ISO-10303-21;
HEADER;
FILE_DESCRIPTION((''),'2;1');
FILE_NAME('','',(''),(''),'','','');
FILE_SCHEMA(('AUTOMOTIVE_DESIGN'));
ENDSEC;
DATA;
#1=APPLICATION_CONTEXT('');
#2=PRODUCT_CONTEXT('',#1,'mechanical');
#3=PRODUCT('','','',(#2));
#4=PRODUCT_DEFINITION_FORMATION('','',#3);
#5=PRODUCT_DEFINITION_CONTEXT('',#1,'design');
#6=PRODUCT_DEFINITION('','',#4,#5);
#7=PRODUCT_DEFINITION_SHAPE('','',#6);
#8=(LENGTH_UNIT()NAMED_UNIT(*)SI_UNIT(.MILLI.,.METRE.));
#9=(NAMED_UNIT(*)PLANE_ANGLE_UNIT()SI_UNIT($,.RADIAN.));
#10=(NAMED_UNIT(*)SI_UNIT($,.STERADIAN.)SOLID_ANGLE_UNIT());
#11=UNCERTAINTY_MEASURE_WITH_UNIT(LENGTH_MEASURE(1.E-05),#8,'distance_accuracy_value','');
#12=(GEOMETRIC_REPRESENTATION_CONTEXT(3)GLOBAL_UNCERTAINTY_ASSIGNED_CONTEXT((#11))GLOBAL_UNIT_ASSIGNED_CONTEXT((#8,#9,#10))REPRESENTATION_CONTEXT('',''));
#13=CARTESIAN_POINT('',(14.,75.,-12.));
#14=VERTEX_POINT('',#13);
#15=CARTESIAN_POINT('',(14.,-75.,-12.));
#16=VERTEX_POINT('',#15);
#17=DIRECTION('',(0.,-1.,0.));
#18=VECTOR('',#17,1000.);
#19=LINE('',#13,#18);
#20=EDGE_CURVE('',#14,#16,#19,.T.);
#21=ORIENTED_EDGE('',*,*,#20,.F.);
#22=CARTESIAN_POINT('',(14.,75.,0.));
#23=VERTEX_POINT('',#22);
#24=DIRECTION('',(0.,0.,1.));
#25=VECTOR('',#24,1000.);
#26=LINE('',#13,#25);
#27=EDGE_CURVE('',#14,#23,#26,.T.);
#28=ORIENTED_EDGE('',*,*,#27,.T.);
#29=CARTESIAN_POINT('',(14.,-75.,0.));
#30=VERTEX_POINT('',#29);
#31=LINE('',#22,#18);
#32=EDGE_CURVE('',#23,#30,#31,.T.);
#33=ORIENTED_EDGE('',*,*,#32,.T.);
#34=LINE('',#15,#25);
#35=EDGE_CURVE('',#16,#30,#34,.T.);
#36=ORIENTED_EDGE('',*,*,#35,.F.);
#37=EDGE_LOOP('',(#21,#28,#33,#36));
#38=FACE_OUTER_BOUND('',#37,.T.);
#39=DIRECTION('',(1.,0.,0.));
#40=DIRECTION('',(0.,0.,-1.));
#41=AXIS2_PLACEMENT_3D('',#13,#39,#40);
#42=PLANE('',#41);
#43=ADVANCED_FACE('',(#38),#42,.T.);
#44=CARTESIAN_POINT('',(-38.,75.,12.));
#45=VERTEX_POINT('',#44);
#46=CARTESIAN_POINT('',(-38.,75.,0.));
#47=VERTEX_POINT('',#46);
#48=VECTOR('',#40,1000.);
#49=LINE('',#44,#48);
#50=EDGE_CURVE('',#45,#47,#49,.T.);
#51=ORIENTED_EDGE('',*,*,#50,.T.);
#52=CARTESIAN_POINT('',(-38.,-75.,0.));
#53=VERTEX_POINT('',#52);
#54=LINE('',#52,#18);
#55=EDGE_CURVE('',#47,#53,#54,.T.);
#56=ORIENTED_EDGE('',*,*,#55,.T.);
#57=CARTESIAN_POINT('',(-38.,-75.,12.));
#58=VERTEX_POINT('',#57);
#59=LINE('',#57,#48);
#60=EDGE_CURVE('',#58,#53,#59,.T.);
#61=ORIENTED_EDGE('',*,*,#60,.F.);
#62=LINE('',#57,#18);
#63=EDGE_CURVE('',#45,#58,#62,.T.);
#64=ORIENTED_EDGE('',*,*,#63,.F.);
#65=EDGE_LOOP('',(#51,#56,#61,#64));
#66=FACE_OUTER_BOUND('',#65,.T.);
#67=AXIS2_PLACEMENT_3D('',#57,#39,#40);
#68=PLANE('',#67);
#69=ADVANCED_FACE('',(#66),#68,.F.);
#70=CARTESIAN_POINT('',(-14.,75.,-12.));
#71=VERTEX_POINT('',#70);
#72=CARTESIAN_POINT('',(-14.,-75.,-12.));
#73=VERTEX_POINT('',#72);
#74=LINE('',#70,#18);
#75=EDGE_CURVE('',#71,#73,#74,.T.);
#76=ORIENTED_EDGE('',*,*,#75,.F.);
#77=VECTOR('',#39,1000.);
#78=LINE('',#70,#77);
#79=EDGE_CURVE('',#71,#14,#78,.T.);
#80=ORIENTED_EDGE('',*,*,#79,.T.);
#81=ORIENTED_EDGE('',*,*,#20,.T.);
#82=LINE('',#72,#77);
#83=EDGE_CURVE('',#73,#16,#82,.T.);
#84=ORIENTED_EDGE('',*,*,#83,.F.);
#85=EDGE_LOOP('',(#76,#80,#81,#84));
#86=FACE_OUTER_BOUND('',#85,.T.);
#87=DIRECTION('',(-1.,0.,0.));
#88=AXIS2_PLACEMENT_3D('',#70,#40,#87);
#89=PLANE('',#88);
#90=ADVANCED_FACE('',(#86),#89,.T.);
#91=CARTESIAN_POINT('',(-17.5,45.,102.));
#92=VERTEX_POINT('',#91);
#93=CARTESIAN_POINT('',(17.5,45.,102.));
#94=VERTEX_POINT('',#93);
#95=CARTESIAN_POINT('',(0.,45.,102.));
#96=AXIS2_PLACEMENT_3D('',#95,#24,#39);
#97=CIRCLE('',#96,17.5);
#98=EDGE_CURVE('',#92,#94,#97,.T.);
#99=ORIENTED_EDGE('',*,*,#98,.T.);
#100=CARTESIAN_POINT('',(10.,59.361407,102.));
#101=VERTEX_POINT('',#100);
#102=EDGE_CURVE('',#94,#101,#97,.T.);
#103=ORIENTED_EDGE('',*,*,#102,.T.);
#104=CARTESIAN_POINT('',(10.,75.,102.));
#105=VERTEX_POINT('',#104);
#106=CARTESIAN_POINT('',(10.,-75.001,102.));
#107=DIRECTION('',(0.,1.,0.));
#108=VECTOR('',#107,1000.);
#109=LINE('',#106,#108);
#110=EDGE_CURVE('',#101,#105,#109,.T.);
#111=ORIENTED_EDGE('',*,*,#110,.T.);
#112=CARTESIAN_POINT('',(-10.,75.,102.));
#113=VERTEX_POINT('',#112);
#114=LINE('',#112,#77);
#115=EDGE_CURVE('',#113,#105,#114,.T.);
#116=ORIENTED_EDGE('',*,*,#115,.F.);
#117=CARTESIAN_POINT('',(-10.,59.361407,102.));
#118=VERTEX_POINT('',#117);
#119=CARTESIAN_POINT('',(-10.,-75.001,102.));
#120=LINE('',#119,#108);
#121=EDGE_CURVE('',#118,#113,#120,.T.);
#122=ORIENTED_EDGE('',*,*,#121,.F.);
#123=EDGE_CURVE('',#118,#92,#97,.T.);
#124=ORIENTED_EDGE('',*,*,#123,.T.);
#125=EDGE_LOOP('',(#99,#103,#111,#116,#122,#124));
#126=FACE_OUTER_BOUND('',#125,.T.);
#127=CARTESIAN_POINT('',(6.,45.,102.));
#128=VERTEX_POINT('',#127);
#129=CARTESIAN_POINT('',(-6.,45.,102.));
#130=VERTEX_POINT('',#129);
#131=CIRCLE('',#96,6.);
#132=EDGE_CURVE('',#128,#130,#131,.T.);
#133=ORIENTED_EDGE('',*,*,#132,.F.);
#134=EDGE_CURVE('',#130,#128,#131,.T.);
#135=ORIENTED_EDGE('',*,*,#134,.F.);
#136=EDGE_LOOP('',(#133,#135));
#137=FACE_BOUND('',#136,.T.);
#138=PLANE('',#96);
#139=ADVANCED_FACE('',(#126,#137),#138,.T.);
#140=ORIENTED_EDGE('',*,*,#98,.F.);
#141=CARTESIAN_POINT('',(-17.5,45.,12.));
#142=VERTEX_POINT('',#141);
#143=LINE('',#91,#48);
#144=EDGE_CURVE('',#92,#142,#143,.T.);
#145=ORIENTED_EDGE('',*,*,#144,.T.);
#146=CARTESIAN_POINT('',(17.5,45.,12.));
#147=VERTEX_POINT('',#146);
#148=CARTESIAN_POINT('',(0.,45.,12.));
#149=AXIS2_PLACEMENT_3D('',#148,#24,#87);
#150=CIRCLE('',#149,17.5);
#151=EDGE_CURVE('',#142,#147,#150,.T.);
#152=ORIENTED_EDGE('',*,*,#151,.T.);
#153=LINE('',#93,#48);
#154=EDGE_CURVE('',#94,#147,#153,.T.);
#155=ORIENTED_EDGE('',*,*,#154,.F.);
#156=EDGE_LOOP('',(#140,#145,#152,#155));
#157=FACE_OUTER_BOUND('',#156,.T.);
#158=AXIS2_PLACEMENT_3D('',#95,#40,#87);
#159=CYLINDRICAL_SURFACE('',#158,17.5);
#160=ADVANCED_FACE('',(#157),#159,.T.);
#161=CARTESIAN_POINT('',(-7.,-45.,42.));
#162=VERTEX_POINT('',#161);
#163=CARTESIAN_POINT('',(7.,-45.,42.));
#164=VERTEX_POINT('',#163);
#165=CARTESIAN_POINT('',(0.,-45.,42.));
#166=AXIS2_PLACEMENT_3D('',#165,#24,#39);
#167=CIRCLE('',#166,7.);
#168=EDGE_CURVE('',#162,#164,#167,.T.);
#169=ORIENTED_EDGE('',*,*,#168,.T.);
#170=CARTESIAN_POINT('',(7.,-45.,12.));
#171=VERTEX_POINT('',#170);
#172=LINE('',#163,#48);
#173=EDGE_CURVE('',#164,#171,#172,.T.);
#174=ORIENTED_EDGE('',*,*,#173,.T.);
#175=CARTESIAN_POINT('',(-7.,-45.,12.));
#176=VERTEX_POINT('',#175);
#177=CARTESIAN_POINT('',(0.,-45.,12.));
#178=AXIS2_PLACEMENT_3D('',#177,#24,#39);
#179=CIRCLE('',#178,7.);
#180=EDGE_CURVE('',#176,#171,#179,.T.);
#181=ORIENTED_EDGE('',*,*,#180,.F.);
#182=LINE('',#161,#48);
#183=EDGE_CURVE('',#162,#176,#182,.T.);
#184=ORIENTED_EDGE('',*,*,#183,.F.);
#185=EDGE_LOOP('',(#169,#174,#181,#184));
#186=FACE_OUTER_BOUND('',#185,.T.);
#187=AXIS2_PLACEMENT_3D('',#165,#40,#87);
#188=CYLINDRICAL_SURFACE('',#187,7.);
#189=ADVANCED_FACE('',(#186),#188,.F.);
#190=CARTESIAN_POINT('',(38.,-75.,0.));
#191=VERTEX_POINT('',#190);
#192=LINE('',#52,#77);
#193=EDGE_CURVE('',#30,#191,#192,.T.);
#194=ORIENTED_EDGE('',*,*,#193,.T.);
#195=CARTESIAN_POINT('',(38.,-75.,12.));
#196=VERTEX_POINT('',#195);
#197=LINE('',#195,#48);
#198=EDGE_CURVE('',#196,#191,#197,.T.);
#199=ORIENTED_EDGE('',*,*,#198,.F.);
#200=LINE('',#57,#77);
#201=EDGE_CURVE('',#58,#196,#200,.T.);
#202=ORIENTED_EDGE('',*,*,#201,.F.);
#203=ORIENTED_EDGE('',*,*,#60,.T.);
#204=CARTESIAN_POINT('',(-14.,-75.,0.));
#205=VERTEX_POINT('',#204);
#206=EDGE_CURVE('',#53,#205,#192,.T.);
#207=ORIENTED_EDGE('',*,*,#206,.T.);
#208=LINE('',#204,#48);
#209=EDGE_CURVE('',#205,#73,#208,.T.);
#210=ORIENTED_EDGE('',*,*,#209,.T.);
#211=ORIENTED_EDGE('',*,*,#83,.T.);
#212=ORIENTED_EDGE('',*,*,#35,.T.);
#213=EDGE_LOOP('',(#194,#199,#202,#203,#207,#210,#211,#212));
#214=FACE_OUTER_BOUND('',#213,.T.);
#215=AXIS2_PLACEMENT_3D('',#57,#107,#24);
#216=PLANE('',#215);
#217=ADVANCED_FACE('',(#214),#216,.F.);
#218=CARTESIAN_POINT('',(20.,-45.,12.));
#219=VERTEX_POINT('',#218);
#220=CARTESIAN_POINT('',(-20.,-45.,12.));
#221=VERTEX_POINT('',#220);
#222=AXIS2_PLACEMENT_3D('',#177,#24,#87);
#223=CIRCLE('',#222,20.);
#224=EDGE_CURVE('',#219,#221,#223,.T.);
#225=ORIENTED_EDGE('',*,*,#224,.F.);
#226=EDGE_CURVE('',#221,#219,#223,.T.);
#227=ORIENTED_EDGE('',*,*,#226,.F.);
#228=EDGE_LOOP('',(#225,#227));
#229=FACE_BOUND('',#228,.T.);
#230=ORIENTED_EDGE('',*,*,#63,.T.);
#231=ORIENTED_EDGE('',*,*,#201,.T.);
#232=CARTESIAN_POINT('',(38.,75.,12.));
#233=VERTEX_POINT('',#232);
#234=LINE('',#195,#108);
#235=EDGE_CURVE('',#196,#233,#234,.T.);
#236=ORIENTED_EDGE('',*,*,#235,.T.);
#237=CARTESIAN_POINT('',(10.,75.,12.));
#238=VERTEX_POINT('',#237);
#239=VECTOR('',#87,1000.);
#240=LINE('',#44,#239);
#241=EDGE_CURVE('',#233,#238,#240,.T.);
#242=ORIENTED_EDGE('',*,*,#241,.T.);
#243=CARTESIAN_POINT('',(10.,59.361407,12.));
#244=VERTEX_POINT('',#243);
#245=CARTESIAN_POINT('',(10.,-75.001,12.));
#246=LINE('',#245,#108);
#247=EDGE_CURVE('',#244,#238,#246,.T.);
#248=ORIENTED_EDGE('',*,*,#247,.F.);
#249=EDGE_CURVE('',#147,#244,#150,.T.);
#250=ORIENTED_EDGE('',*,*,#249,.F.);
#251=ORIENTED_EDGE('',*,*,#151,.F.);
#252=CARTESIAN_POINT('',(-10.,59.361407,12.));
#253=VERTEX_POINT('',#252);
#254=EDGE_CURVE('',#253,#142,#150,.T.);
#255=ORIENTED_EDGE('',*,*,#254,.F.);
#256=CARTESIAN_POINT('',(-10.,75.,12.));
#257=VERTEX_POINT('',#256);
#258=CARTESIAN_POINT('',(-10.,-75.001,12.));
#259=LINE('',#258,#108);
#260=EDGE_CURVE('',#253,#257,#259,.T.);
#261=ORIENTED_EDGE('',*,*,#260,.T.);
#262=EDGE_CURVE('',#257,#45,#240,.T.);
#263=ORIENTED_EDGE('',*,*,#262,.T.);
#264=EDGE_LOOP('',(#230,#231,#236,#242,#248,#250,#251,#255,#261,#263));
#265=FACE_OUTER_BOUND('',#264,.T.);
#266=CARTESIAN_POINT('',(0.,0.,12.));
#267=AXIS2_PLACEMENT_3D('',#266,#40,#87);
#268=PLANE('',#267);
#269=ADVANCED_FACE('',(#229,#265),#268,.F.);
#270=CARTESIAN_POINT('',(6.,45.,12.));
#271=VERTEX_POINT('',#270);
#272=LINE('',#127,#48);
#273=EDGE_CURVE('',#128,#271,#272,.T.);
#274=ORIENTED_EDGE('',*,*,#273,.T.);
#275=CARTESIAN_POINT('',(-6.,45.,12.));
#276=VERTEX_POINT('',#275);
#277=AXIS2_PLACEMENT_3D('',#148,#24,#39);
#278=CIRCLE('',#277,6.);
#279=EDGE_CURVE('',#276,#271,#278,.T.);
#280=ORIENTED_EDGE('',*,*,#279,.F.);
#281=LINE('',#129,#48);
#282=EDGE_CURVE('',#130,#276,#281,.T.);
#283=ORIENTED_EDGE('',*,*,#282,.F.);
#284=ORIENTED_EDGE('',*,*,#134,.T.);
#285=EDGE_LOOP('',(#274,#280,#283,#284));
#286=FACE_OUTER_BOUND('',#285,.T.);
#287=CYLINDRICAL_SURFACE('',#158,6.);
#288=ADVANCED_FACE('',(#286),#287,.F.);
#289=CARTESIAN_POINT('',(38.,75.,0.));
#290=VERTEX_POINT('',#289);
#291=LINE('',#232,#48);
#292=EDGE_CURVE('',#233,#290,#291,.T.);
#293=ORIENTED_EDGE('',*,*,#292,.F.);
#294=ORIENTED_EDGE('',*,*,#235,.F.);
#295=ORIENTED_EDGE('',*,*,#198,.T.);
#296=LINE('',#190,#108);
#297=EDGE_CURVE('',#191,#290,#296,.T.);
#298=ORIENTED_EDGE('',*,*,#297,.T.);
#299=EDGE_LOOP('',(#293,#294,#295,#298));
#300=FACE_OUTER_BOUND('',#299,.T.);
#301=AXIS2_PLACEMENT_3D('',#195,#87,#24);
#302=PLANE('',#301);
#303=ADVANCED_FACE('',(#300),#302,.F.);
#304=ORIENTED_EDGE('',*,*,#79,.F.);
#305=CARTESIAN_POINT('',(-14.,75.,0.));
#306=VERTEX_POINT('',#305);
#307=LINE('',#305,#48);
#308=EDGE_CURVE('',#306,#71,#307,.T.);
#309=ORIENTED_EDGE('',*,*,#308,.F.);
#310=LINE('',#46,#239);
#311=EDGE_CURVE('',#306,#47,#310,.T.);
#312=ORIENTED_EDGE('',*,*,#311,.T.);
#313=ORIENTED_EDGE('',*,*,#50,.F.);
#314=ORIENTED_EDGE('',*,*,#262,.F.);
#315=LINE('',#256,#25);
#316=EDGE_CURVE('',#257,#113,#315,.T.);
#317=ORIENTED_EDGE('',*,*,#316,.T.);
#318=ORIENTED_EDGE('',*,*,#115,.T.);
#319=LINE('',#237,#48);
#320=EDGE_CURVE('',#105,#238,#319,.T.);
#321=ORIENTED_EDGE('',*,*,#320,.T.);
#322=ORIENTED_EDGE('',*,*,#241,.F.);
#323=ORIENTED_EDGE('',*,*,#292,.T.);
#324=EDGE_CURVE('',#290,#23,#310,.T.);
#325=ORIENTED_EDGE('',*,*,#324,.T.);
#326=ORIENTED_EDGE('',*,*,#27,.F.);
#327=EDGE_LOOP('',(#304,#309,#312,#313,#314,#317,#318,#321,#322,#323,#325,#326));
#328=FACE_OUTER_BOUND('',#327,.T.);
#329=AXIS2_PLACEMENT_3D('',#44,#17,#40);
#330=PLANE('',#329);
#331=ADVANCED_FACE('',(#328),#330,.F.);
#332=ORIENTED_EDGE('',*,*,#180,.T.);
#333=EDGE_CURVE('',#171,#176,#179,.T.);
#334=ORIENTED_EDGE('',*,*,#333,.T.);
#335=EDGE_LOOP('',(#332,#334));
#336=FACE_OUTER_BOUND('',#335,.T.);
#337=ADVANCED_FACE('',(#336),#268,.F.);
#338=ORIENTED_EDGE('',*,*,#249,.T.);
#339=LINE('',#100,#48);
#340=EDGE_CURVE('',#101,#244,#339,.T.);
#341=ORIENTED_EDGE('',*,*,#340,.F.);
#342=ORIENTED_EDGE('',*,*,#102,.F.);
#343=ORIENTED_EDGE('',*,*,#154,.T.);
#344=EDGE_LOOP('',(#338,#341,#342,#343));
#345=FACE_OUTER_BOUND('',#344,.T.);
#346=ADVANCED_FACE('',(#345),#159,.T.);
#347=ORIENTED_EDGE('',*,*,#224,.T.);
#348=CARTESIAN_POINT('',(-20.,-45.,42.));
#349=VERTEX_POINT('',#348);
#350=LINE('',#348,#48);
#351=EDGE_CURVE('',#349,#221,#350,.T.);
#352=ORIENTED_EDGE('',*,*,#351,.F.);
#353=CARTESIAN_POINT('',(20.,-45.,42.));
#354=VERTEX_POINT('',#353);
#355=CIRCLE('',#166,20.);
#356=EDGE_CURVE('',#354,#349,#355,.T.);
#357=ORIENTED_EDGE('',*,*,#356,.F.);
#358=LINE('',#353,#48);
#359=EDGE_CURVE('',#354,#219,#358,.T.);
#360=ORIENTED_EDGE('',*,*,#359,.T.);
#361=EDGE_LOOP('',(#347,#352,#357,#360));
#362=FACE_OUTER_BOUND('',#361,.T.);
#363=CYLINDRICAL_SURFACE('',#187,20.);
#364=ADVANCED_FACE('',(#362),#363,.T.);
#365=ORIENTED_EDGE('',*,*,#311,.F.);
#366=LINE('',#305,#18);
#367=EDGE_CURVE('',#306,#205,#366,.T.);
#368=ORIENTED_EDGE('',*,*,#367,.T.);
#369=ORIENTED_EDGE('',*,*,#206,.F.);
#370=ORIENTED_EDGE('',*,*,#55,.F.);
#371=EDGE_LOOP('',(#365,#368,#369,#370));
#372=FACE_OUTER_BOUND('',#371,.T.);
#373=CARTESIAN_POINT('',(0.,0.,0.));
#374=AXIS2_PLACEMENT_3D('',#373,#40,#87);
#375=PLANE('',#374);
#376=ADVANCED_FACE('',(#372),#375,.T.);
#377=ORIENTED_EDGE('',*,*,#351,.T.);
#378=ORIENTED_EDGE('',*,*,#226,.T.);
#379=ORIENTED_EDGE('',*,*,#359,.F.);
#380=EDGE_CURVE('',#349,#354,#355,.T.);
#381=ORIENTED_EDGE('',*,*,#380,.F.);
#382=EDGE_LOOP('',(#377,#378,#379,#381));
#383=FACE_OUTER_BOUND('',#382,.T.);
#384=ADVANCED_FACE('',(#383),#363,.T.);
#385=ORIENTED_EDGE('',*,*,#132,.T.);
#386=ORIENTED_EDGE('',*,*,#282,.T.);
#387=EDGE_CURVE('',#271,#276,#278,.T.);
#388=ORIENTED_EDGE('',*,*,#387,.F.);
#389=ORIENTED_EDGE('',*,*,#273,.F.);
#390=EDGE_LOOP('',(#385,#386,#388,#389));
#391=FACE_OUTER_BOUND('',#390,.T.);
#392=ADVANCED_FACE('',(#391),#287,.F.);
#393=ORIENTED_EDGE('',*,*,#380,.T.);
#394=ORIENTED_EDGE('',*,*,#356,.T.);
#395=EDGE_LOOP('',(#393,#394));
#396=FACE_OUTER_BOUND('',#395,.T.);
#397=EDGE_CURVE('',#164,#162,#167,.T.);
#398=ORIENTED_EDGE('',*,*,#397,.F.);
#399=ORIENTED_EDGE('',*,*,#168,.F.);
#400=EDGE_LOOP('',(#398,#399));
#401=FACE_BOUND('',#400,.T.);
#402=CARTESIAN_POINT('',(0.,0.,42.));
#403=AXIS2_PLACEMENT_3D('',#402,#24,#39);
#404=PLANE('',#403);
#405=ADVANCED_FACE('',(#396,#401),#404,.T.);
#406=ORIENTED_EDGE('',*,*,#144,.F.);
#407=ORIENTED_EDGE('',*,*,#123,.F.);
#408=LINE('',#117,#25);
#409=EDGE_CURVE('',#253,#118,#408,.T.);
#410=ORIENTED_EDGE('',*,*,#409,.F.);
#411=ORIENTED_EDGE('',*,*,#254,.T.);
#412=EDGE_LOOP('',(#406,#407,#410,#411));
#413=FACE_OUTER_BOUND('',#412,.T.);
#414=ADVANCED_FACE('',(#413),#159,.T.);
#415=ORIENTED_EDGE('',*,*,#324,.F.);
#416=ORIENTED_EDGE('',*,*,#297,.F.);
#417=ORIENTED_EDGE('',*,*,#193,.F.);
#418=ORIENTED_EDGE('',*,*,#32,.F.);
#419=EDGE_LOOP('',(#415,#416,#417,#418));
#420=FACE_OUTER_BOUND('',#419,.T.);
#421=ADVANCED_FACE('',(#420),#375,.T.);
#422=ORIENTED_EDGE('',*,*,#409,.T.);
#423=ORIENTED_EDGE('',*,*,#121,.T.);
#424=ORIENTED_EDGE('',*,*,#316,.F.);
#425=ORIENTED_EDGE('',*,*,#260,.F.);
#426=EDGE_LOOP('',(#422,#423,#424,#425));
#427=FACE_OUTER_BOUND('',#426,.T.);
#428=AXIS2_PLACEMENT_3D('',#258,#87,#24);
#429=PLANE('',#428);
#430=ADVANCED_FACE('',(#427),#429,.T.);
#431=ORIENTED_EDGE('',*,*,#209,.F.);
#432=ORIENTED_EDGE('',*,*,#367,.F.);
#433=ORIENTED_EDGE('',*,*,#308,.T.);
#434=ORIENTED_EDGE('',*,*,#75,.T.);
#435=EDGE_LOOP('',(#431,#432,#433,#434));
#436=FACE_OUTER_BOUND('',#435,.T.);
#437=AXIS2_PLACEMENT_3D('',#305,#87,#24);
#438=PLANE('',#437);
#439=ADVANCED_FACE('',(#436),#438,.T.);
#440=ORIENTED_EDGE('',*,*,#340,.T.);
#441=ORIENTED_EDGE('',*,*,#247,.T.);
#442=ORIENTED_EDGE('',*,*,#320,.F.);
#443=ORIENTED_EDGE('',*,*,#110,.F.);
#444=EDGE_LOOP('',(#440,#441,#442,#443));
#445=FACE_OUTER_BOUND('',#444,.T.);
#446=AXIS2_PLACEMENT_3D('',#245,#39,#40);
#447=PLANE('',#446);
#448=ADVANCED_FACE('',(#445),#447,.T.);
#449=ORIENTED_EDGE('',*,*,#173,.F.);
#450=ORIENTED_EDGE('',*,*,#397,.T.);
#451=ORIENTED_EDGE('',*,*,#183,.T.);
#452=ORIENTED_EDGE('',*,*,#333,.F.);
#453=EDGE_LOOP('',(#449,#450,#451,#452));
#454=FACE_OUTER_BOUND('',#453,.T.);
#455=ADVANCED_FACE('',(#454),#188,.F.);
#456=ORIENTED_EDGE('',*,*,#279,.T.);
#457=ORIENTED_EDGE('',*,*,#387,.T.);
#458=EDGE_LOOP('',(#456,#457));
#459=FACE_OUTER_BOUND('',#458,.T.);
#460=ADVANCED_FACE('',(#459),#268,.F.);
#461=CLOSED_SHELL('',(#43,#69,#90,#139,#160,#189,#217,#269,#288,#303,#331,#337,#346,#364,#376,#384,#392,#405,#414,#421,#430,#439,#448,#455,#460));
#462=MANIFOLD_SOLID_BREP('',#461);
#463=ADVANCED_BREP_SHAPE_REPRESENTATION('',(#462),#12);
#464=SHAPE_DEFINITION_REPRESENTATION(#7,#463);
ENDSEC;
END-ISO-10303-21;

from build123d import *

# Parameters (mm, degrees)
BASE_PLATE_SKETCH_W           = 76
BASE_PLATE_SKETCH_H           = 150
BASE_PLATE_DEPTH              = 12
TOP_TAB_SKETCH_W              = 28
TOP_TAB_SKETCH_H              = 12
TOP_TAB_DEPTH                 = 150
LOWER_BUSHING_BOSS_SKETCH_R   = 20
LOWER_BUSHING_BOSS_SKETCH_R_2 = 7
LOWER_BUSHING_BOSS_DEPTH      = 30
UPPER_ARM_SKETCH_R            = 17.5
UPPER_ARM_SKETCH_R_2          = 6
UPPER_ARM_DEPTH               = 90
ARM_RIB_REACH                 = 187.332
ARM_RIB_END_RADIUS            = 17.5
ARM_RIB_SKETCH_W              = 20
ARM_RIB_SKETCH_H              = 90


with BuildPart() as part:
    # Base Plate Sketch → Base Plate (new body)
    with BuildSketch(Plane.XY):
        Rectangle(BASE_PLATE_SKETCH_W, BASE_PLATE_SKETCH_H)
    extrude(amount=BASE_PLATE_DEPTH)

    # Top Tab Sketch → Top Tab (add, through all)
    with BuildSketch(Plane.XZ.offset(75)):
        with Locations((0, -6)):
            Rectangle(TOP_TAB_SKETCH_W, TOP_TAB_SKETCH_H)
    extrude(amount=-TOP_TAB_DEPTH)

    # Lower Bushing Boss Sketch → Lower Bushing Boss (add)
    with BuildSketch(Plane.XY.offset(12)):
        with Locations(Location((0, -45, 0), (0, 0, 180))):
            Circle(LOWER_BUSHING_BOSS_SKETCH_R)
        with Locations((0, -45)):
            Circle(LOWER_BUSHING_BOSS_SKETCH_R_2, mode=Mode.SUBTRACT)
    extrude(amount=LOWER_BUSHING_BOSS_DEPTH)

    # Upper Arm Sketch → Upper Arm (add)
    with BuildSketch(Plane.XY.offset(12)):
        with Locations(Location((0, 45, 0), (0, 0, 180))):
            Circle(UPPER_ARM_SKETCH_R)
        with Locations(Location((0, 45, 0), (0, 0, 180))):
            Circle(UPPER_ARM_SKETCH_R_2, mode=Mode.SUBTRACT)
    extrude(amount=UPPER_ARM_DEPTH)

    # Arm Rib: up to this cylinder (the profile starts outside it)
    arm_rib_end = Plane(origin=(0, 45, 57), z_dir=(0, 0, -1)) * Cylinder(ARM_RIB_END_RADIUS, 410.664, mode=Mode.PRIVATE)
    # Arm Rib Sketch → Arm Rib (add, up to the surface)
    with BuildSketch(Plane(origin=(0, 75, 0), x_dir=(1, 0, 0), z_dir=(0, 1, 0)), mode=Mode.PRIVATE) as arm_rib_sk1:
        with Locations((0, -57)):
            Rectangle(ARM_RIB_SKETCH_W, ARM_RIB_SKETCH_H)
    arm_rib_tool1 = extrude(arm_rib_sk1.sketch, amount=-ARM_RIB_REACH, mode=Mode.PRIVATE) - arm_rib_end
    add(arm_rib_tool1.solids().sort_by_distance((0, 75, 57))[0])


solid = part.part
